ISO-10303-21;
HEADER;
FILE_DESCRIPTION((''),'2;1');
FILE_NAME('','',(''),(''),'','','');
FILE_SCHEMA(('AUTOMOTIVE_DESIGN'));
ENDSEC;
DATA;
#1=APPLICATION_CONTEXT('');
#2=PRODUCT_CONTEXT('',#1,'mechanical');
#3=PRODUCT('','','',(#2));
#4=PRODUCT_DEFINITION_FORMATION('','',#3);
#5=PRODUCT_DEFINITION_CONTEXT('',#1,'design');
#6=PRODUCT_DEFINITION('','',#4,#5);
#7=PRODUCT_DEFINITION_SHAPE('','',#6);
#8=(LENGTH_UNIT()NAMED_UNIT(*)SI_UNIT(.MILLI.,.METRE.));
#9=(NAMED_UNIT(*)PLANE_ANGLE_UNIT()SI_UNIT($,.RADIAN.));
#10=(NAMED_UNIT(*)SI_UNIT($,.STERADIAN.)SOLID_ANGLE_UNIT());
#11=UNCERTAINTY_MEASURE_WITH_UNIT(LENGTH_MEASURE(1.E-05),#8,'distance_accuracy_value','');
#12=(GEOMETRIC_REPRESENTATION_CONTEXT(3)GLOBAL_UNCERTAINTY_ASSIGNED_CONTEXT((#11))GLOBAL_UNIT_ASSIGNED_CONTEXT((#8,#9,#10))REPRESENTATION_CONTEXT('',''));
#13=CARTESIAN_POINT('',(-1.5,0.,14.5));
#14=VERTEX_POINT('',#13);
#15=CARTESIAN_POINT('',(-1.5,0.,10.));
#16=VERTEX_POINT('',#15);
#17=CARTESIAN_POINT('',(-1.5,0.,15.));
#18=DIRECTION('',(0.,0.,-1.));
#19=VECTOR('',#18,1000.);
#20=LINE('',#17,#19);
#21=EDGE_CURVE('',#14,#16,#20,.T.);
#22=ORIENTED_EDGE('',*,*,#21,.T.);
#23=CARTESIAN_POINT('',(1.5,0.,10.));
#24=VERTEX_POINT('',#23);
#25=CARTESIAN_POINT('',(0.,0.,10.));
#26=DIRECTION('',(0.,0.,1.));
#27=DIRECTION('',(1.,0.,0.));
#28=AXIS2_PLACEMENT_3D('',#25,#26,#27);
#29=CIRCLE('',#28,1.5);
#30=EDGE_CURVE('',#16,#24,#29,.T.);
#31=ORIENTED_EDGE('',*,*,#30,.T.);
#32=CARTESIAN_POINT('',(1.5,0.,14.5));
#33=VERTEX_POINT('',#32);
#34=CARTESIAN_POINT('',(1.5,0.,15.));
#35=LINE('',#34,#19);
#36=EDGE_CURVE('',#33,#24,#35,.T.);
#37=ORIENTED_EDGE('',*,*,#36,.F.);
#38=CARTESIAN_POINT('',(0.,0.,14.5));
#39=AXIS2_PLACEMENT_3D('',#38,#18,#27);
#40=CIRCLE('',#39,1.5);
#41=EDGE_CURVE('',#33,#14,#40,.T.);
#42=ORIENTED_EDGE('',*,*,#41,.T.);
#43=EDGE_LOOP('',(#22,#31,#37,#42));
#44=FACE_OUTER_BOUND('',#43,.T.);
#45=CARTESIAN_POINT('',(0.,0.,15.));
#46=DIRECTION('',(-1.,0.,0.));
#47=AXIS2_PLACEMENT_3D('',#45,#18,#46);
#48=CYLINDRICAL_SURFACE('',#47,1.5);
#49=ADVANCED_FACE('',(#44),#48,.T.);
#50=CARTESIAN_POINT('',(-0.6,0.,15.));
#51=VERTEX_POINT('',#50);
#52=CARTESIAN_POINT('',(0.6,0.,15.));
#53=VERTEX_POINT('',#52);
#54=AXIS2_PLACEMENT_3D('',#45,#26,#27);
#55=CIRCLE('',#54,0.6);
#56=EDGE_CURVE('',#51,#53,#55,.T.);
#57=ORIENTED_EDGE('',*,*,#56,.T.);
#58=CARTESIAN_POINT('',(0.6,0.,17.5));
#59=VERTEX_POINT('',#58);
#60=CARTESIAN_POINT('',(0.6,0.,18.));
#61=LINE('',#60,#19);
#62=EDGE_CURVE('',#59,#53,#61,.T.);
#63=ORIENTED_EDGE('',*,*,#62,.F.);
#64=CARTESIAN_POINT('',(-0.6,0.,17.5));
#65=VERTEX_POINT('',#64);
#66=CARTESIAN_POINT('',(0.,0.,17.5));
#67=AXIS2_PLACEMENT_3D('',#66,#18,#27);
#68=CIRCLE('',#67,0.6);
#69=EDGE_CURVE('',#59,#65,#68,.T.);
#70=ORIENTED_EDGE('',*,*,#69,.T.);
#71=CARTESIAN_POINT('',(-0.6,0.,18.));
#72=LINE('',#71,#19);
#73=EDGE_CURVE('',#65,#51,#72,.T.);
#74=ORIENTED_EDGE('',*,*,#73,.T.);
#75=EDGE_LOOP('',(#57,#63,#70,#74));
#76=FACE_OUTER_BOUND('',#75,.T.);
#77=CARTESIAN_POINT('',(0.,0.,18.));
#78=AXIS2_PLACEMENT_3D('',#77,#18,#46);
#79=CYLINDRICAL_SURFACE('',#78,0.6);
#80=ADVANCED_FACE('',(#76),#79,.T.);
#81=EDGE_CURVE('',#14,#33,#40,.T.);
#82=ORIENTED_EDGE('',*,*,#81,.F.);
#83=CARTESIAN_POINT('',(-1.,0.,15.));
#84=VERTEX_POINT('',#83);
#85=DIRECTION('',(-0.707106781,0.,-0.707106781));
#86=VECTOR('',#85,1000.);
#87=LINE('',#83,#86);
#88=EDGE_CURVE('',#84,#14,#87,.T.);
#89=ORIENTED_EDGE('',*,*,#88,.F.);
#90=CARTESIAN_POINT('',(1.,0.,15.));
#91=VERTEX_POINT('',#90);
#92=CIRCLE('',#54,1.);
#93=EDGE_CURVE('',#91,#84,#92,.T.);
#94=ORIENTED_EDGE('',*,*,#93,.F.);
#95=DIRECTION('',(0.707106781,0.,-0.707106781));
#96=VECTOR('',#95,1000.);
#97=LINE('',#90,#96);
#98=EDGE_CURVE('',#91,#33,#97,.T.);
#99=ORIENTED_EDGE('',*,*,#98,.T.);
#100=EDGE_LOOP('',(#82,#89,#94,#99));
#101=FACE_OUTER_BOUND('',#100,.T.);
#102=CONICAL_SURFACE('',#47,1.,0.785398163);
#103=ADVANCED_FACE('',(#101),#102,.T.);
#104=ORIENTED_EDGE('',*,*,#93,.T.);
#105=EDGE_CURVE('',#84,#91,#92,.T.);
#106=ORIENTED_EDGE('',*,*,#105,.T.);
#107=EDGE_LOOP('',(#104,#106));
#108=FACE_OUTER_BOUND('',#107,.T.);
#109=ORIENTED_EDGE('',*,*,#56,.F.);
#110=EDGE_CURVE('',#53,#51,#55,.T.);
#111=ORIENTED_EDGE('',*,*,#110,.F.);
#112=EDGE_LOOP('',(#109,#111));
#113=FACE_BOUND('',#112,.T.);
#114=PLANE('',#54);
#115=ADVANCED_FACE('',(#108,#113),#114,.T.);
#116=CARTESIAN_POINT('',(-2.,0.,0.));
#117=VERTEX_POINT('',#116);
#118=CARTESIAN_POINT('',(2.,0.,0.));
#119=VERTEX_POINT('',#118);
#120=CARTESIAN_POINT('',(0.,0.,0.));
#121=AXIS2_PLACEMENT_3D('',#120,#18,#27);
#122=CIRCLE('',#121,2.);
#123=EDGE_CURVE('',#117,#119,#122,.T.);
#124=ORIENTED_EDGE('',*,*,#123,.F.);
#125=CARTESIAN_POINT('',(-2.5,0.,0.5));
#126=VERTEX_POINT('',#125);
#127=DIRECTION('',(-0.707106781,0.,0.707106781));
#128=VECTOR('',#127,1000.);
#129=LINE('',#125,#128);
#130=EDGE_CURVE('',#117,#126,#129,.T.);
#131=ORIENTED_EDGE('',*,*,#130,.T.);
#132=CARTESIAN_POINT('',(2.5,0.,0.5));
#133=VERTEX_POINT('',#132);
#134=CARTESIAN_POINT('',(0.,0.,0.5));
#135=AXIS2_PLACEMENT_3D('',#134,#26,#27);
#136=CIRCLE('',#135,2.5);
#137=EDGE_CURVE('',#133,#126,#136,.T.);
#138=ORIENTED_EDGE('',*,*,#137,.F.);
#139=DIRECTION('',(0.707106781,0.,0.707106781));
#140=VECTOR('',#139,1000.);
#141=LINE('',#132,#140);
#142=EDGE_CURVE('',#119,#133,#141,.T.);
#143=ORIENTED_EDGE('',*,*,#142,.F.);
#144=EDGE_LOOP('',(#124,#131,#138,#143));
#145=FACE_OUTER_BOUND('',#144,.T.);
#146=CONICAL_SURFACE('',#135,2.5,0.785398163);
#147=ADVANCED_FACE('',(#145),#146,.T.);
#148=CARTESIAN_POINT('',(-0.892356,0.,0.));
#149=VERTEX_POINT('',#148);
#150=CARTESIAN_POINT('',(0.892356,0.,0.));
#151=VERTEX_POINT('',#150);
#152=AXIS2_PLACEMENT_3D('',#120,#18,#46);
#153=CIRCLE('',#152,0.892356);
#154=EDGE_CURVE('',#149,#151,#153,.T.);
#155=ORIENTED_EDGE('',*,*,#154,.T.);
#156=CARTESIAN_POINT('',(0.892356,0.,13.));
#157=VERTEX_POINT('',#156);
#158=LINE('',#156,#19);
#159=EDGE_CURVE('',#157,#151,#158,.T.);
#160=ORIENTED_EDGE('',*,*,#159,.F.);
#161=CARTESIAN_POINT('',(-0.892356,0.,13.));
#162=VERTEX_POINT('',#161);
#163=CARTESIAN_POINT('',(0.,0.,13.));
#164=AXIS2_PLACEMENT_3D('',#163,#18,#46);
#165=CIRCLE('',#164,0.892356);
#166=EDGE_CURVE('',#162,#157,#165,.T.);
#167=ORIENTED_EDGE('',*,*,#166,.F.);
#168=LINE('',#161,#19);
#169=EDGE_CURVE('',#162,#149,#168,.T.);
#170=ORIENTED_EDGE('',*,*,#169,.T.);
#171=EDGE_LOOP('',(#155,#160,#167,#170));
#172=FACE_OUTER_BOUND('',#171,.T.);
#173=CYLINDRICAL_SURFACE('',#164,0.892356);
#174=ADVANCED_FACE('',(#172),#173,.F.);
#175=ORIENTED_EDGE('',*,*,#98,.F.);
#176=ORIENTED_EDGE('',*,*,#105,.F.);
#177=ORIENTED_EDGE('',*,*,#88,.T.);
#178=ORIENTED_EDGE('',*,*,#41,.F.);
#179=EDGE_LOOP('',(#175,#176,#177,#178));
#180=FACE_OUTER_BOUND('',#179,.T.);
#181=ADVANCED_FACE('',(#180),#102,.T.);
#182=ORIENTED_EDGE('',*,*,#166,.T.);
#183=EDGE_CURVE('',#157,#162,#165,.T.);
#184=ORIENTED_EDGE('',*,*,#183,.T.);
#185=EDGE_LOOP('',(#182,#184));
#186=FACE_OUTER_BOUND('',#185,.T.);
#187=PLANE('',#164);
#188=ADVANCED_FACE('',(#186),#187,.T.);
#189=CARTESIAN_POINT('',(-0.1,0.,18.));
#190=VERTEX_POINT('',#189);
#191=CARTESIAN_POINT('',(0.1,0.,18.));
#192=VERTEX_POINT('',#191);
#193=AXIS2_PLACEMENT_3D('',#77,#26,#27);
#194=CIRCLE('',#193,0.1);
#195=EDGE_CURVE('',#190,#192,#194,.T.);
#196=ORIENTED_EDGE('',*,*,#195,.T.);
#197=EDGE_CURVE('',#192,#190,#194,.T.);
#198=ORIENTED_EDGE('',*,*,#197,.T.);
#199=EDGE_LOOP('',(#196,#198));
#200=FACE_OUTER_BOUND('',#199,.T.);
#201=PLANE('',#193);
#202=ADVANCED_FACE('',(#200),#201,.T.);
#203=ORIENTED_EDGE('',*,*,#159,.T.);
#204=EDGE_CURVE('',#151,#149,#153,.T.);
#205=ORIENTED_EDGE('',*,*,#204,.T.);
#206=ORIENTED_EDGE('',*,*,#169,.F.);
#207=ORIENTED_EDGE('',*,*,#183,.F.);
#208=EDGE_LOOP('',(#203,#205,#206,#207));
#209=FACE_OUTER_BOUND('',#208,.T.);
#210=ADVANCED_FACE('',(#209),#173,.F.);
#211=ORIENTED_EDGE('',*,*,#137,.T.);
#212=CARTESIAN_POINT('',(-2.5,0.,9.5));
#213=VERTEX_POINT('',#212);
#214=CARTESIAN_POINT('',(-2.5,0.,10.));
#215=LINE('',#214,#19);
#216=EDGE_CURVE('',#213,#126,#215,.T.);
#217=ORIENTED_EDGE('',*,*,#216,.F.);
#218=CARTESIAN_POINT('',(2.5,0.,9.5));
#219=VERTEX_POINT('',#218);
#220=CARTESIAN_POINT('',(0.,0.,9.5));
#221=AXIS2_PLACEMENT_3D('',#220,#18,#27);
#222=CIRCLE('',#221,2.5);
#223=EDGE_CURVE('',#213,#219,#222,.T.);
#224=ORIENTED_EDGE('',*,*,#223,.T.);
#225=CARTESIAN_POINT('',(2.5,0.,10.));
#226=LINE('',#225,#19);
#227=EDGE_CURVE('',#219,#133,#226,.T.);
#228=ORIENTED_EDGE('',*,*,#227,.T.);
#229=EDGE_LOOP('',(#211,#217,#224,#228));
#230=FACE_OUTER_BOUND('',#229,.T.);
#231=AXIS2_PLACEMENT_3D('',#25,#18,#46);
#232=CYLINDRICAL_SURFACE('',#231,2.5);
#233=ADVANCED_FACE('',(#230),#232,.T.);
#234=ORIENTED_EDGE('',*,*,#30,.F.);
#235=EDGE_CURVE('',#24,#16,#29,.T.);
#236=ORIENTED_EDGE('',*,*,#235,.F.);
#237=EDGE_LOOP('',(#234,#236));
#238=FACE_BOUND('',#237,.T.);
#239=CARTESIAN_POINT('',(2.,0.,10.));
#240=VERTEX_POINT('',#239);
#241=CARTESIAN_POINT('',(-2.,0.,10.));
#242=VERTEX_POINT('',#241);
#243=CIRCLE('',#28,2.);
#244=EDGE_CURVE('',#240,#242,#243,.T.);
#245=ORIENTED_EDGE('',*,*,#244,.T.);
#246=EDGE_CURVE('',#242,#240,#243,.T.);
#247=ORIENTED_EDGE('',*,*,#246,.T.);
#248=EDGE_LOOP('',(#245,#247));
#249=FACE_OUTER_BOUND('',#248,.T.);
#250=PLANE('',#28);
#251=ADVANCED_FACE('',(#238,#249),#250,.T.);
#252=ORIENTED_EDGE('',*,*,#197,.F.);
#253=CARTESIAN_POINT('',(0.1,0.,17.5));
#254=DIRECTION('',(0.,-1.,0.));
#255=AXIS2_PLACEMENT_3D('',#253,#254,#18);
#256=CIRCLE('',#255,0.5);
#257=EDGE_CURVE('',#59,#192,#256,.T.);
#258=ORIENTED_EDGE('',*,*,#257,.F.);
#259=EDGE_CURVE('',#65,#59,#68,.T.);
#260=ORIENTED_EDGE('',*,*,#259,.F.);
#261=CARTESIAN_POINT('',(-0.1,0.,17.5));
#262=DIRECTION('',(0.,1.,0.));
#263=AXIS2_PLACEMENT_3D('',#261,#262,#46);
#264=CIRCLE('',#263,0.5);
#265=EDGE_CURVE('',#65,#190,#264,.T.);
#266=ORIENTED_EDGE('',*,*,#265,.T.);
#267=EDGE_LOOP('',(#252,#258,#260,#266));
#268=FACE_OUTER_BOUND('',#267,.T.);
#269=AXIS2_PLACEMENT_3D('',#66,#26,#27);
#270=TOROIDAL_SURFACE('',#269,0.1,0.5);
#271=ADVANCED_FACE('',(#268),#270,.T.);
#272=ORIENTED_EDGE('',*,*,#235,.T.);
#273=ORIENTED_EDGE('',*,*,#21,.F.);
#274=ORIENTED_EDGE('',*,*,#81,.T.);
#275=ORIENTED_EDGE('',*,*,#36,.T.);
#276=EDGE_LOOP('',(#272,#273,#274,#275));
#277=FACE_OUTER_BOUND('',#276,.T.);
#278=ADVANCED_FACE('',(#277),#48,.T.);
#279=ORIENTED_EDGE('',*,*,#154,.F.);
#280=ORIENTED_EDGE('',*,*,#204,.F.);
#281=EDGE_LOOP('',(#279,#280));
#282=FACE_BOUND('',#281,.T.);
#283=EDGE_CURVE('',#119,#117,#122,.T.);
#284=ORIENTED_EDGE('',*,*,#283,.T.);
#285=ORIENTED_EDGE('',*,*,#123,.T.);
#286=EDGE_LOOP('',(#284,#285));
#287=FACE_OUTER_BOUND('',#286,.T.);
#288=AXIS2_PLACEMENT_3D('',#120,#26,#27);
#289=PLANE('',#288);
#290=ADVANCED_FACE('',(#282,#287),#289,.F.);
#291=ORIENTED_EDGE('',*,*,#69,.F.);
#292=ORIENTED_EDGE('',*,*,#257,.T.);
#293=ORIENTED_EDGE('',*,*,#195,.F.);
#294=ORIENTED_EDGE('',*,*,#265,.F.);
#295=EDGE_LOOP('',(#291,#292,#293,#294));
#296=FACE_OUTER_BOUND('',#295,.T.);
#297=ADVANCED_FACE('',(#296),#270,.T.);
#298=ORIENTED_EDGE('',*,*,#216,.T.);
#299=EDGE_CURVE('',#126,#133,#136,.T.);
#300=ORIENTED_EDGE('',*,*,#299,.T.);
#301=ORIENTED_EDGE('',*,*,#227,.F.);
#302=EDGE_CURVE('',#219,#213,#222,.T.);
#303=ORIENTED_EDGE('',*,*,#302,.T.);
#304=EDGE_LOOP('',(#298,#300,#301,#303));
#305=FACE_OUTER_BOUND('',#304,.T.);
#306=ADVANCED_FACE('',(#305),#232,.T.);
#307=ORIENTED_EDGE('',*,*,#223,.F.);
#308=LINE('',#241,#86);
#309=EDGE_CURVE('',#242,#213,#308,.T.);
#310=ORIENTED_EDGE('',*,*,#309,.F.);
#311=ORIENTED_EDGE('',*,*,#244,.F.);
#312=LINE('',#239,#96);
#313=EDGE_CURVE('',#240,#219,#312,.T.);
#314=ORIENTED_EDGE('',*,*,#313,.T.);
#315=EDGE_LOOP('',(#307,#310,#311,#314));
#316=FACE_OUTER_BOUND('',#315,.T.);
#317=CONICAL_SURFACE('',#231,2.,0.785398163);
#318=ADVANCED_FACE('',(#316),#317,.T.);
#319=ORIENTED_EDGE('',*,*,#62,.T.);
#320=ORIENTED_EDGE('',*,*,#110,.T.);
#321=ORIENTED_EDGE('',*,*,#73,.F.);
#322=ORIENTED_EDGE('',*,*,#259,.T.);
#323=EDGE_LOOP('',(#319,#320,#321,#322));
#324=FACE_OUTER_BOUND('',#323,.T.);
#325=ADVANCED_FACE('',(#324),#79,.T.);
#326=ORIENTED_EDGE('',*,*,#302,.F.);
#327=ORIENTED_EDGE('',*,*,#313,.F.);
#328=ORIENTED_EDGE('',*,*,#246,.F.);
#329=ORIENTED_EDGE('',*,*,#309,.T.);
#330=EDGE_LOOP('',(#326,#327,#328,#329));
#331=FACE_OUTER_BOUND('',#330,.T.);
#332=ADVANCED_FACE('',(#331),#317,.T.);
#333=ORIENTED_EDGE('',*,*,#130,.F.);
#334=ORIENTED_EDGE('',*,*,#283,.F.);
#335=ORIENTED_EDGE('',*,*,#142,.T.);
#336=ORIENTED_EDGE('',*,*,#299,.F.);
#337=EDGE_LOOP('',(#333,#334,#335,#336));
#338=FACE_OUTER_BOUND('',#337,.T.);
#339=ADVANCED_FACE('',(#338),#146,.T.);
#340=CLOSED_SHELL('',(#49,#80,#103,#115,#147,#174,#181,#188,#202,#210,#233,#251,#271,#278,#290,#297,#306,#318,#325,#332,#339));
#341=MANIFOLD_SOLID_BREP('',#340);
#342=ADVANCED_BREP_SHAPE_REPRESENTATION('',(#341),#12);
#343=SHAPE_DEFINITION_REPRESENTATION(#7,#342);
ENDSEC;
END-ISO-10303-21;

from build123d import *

# Parameters (mm, degrees)
SKETCH1_R           = 2.5
BOSS_EXTRUDE1_DEPTH = 10
SKETCH2_R           = 1.5
BOSS_EXTRUDE2_DEPTH = 5
SKETCH3_R           = 0.6
BOSS_EXTRUDE3_DEPTH = 3
FILLET1_R           = 0.5
SKETCH4_R           = 0.892356389
CUT_EXTRUDE1_DEPTH  = 13
CHAMFER1_SIZE       = 0.5


with BuildPart() as part:
    # Sketch1 → Boss-Extrude1 (new body)
    with BuildSketch(Plane.XY):
        Circle(SKETCH1_R)
    extrude(amount=BOSS_EXTRUDE1_DEPTH)

    # Sketch2 → Boss-Extrude2 (add)
    with BuildSketch(Plane.XY.offset(10)):
        Circle(SKETCH2_R)
    extrude(amount=BOSS_EXTRUDE2_DEPTH)

    # Sketch3 → Boss-Extrude3 (add)
    with BuildSketch(Plane.XY.offset(15)):
        Circle(SKETCH3_R)
    extrude(amount=BOSS_EXTRUDE3_DEPTH)

    # Fillet1
    fillet1_edges = [part.edges().sort_by_distance(p)[0] for p in [
        (-0.6, 0, 18),
    ]]
    fillet(fillet1_edges, radius=FILLET1_R)

    # Sketch4 → Cut-Extrude1 (cut)
    with BuildSketch(Plane(origin=(0, 0, 0), x_dir=(-1, 0, 0), z_dir=(0, 0, -1))):
        Circle(SKETCH4_R)
    extrude(amount=-CUT_EXTRUDE1_DEPTH, mode=Mode.SUBTRACT)

    # Chamfer1
    chamfer1_edges = [part.edges().sort_by_distance(p)[0] for p in [
        (-2.5, 0, 0),
        (-2.5, 0, 10),
        (-1.5, 0, 15),
    ]]
    chamfer(chamfer1_edges, length=CHAMFER1_SIZE)


solid = part.part
